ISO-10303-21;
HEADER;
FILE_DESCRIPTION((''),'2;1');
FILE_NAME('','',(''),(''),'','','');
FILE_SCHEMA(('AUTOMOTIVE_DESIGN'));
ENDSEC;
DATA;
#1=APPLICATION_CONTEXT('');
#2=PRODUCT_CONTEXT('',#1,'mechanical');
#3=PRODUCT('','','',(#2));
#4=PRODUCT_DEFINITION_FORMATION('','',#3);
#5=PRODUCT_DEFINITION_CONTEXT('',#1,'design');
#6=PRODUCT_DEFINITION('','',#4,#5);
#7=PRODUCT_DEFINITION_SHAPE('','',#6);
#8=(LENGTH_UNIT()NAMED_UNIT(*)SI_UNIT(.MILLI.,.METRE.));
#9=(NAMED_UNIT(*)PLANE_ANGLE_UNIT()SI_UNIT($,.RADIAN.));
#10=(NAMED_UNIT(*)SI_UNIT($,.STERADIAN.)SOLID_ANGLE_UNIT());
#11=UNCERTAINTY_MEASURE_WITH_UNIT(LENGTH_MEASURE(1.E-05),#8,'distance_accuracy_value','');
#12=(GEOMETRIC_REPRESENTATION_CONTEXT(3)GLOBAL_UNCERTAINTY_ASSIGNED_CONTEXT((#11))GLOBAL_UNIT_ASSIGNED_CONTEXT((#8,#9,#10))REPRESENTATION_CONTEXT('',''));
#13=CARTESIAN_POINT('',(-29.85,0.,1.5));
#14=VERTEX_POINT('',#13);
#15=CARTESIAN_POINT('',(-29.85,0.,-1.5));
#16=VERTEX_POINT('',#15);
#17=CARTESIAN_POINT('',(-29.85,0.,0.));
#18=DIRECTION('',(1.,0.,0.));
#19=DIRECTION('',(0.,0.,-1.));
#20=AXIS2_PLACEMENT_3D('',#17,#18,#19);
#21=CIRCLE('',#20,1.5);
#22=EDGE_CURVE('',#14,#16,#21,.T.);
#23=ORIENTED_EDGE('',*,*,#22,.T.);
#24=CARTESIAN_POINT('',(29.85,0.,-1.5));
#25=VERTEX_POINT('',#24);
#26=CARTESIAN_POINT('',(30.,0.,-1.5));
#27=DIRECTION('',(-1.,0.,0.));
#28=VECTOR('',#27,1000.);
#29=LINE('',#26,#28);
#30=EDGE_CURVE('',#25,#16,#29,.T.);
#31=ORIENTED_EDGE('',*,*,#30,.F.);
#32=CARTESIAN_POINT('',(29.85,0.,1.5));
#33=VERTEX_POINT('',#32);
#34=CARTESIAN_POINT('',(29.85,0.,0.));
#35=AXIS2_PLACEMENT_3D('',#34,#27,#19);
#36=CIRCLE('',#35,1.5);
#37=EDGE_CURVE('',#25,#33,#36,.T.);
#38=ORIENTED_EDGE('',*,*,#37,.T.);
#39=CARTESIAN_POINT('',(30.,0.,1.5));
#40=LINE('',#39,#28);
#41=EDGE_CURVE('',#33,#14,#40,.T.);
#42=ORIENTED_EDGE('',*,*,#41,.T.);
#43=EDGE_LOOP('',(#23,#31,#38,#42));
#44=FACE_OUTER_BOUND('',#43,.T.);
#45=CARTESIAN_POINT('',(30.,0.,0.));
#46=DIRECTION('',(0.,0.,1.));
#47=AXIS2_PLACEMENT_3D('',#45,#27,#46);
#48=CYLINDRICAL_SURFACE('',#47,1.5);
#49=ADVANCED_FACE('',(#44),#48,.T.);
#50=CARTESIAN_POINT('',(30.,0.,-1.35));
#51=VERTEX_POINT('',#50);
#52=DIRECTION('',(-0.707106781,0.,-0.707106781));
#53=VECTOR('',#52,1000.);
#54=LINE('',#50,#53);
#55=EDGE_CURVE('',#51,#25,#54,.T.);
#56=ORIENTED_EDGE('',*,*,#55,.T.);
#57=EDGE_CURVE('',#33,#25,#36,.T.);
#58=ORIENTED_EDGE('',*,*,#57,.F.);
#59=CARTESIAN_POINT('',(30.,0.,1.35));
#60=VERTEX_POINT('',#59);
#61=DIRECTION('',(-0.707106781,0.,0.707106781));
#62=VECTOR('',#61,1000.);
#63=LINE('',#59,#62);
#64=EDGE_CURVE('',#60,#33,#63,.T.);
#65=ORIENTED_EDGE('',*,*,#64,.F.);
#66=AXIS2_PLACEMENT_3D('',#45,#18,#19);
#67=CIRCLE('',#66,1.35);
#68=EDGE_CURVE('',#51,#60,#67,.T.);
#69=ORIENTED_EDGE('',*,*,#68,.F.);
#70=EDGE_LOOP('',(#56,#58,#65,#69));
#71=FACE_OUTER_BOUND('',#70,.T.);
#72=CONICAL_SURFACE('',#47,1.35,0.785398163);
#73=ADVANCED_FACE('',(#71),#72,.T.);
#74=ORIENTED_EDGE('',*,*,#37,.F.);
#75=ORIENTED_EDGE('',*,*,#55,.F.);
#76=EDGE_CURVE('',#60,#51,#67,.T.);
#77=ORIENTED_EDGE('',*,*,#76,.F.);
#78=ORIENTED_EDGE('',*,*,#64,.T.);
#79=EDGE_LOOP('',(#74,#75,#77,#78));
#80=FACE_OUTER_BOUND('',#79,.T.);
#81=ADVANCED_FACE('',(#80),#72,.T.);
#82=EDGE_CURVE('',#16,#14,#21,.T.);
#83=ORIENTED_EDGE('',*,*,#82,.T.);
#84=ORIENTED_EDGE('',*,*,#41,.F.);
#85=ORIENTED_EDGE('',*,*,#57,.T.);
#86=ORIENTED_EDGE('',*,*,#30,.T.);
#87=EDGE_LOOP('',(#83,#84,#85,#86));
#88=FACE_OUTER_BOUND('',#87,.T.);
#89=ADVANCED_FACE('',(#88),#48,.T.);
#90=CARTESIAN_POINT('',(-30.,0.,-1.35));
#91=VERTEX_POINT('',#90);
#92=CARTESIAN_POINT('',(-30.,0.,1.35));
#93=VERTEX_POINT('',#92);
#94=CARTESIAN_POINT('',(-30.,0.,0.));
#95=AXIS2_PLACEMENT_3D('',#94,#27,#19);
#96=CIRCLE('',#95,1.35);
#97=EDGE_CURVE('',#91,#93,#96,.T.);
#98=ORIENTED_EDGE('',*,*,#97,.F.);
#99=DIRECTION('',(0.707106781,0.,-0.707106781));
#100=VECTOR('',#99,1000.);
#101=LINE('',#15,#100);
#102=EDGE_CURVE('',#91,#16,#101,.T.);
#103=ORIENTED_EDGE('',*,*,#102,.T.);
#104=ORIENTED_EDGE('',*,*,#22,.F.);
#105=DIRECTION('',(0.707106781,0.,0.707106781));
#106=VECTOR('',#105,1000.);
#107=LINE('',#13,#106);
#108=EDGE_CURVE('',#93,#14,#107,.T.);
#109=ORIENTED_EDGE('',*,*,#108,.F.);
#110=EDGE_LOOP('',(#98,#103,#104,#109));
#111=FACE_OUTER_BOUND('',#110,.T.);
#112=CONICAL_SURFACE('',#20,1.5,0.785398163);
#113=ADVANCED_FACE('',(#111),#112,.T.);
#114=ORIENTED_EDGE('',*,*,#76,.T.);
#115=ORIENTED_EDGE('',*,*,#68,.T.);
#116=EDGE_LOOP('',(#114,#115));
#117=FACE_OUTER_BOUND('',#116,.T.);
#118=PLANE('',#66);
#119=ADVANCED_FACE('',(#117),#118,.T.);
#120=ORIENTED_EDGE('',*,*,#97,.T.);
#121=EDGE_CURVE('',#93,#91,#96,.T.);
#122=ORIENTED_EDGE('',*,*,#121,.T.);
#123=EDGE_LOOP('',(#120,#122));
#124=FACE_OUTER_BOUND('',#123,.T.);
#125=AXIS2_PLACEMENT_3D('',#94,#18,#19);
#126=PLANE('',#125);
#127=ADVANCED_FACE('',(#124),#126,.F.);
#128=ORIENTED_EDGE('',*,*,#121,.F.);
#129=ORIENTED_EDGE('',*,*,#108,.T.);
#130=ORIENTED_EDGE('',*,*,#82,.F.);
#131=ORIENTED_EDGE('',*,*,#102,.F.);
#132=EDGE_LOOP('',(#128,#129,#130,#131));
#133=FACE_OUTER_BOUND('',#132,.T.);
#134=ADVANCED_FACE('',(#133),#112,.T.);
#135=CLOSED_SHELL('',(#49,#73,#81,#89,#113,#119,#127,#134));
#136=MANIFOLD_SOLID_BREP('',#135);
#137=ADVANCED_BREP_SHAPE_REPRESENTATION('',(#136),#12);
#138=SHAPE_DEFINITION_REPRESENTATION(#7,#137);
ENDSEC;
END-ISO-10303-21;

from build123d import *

# Parameters (mm, degrees)
SKETCH_1_R           = 1.5
EXTRUDE_1_DEPTH      = 30
CHAMFER_C0_15_1_SIZE = 0.15


with BuildPart() as part:
    # 草图1 → 凸台-拉伸1 (new, symmetric)
    with BuildSketch(Plane(origin=(0, 0, 0), x_dir=(0, 0, -1), z_dir=(1, 0, 0))):
        Circle(SKETCH_1_R)
    extrude(amount=EXTRUDE_1_DEPTH, both=True)

    # C0.15 倒角1
    chamfer_c0_15_1_edges = [part.edges().sort_by_distance(p)[0] for p in [
        (-30, 0, 1.5),
        (30, 0, 1.5),
    ]]
    chamfer(chamfer_c0_15_1_edges, length=CHAMFER_C0_15_1_SIZE)


solid = part.part
